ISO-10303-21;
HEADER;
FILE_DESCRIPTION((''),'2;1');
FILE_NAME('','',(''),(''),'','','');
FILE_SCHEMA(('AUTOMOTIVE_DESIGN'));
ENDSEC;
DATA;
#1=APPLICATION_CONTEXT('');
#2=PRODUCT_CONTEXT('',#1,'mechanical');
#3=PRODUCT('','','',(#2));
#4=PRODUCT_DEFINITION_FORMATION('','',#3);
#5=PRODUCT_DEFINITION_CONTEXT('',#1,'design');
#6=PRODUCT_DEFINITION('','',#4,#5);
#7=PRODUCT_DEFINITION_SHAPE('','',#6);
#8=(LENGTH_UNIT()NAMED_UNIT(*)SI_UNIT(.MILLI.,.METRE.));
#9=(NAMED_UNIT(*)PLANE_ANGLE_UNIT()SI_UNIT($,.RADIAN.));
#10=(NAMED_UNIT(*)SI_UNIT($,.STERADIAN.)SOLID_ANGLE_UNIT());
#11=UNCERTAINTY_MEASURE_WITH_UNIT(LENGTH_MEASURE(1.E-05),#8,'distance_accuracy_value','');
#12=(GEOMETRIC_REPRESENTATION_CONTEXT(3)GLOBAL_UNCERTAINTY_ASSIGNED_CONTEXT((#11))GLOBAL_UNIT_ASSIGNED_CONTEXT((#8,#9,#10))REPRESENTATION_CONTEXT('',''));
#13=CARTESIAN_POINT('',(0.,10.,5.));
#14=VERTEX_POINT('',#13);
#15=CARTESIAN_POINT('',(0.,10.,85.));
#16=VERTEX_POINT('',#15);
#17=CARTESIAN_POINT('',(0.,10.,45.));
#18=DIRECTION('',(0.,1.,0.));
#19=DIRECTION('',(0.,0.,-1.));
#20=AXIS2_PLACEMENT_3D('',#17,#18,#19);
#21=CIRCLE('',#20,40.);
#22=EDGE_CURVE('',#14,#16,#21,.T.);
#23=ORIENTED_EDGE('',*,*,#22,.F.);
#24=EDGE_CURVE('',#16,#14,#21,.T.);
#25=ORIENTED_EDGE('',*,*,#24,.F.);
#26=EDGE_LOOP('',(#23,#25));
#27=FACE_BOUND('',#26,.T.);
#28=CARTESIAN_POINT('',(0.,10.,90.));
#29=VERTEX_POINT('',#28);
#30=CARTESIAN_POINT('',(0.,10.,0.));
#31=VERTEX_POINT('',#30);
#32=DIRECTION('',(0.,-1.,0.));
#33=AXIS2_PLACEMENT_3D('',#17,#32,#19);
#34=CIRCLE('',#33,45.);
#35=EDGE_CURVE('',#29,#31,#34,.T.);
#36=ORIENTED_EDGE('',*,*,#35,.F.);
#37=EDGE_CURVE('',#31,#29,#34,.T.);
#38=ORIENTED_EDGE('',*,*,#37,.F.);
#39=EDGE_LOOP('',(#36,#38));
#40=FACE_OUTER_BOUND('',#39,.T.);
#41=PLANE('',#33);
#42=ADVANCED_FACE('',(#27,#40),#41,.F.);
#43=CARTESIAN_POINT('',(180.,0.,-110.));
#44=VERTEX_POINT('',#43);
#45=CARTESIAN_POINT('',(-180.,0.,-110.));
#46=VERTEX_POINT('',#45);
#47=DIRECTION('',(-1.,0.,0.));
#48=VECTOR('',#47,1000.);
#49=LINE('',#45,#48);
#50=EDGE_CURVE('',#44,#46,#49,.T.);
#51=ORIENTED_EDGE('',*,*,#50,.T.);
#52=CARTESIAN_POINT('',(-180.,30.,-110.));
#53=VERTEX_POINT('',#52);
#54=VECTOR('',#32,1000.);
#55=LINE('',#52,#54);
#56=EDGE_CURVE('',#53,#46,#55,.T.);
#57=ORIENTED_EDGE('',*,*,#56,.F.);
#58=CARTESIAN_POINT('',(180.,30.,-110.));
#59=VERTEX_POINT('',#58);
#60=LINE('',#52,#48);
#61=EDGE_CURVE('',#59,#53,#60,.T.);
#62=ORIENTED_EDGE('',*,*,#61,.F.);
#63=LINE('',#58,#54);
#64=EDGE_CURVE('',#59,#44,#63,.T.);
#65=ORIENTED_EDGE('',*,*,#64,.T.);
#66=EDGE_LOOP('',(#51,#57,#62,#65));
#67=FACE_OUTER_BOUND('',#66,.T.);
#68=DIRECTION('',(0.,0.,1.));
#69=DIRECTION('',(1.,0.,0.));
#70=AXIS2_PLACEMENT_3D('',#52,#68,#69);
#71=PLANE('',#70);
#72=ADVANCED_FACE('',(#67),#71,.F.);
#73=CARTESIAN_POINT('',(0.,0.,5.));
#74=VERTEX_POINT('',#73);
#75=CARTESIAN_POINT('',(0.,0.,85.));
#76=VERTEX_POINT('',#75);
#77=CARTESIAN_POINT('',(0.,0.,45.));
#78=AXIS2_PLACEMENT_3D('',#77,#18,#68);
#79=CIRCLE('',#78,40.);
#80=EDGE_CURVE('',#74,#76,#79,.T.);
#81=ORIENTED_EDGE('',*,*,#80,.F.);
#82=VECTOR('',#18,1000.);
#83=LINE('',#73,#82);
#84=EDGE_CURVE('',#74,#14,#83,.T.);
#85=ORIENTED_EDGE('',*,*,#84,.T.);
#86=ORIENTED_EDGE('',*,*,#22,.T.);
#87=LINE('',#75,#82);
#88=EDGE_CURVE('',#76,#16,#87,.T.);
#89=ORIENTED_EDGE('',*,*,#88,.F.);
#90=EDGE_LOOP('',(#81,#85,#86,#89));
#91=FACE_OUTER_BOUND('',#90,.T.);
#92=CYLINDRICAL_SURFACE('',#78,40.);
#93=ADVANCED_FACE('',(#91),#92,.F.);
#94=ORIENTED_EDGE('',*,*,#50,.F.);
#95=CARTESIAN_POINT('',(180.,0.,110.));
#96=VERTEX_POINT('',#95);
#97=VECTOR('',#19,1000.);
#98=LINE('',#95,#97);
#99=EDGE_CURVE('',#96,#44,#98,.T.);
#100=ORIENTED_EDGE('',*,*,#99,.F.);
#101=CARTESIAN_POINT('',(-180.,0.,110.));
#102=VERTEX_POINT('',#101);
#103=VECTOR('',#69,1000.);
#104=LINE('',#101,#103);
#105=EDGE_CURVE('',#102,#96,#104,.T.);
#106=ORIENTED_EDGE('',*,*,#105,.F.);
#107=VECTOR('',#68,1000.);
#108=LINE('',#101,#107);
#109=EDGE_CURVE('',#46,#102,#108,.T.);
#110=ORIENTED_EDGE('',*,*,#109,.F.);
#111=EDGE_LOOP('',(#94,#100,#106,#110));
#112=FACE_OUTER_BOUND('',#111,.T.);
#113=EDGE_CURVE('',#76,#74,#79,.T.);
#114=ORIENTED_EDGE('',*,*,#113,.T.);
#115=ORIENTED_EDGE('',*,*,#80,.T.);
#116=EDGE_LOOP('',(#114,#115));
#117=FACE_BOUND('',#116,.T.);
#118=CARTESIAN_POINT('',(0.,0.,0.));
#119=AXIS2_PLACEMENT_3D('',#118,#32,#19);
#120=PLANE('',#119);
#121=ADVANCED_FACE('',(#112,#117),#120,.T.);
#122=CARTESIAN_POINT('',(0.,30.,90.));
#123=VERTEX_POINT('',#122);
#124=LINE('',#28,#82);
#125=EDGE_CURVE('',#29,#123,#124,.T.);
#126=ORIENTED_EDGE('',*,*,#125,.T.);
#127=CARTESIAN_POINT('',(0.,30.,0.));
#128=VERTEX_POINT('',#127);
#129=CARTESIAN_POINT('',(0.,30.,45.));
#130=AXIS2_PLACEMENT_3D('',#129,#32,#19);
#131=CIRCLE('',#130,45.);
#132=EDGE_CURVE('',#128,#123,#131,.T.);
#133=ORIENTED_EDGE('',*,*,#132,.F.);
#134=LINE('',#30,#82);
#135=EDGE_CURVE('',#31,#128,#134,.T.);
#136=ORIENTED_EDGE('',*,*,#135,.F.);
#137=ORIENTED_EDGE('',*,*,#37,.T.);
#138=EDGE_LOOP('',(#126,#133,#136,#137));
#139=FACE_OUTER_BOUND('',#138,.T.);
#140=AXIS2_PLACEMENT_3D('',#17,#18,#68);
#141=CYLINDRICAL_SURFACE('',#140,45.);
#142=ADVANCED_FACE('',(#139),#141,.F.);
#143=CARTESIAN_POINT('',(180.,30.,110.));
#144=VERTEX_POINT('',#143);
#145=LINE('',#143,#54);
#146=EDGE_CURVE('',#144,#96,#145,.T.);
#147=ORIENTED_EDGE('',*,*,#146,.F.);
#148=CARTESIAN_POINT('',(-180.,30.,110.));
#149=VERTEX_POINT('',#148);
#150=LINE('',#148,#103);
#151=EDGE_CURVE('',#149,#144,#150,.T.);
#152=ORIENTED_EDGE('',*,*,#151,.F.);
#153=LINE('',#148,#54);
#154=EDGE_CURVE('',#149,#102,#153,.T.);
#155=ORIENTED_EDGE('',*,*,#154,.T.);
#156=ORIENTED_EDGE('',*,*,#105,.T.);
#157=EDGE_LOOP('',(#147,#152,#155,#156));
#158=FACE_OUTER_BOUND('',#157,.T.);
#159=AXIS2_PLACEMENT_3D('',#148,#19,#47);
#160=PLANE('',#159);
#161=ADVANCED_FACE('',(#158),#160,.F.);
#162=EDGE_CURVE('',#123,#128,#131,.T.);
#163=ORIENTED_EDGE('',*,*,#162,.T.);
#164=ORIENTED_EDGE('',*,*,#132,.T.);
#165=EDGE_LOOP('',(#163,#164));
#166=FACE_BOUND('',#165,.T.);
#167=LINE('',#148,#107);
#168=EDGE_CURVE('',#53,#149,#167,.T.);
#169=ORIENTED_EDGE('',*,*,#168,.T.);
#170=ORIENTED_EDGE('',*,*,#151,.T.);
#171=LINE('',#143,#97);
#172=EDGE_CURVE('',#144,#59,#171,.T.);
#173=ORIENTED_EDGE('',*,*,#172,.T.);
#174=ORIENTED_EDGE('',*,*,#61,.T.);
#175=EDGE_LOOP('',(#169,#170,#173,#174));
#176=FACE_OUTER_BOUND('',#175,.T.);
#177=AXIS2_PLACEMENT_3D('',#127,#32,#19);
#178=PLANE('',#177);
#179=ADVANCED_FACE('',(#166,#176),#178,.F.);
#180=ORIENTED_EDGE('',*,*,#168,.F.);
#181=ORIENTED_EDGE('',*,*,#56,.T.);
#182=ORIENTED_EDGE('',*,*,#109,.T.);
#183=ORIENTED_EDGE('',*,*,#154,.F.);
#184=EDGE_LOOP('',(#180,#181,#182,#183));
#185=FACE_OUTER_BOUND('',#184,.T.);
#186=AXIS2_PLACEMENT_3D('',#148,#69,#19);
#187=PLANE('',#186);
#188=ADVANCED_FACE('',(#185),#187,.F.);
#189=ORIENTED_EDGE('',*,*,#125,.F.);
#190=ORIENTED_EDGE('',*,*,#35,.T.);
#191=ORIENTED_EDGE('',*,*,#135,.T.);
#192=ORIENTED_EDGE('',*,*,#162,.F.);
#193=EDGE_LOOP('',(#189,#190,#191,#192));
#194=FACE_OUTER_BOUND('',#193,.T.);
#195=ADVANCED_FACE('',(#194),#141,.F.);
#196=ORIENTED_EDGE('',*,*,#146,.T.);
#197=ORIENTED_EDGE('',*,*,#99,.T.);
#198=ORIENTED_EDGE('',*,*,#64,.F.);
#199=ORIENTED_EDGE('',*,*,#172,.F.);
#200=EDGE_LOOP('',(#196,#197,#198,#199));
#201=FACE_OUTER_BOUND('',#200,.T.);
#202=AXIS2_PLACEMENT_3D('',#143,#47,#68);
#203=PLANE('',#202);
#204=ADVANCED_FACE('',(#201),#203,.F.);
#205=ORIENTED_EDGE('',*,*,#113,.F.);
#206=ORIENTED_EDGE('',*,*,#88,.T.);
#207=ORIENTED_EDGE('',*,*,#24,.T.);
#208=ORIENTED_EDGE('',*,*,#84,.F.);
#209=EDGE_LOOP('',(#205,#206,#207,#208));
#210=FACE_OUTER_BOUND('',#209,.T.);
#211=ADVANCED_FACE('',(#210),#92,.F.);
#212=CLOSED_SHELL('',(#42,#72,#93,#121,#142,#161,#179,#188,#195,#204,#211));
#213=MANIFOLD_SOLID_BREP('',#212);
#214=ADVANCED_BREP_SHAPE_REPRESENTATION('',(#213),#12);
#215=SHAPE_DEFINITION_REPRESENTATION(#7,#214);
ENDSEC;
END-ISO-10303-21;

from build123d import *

# Parameters (mm, degrees)
SKETCH_1_W          = 360
SKETCH_1_H          = 220
EXTRUDE_1_DEPTH     = 30
SKETCH_2_R          = 40
CUT_EXTRUDE_1_DEPTH = 214.072757527
SKETCH_3_R          = 45
CUT_EXTRUDE_2_DEPTH = 20


with BuildPart() as part:
    # 草图1 → 凸台-拉伸1 (new body)
    with BuildSketch(Plane(origin=(0, 0, 0), x_dir=(1, 0, 0), z_dir=(0, 1, 0))):
        Rectangle(SKETCH_1_W, SKETCH_1_H)
    extrude(amount=EXTRUDE_1_DEPTH)

    # 草图2 → 切除-拉伸1 (cut, through all)
    with BuildSketch(Plane(origin=(0, 30, 0), x_dir=(1, 0, 0), z_dir=(0, 1, 0))):
        with Locations(Location((0, -45, 0), (0, 0, 270))):
            Circle(SKETCH_2_R)
    extrude(amount=-CUT_EXTRUDE_1_DEPTH, mode=Mode.SUBTRACT)

    # 草图3 → 切除-拉伸2 (cut)
    with BuildSketch(Plane.XZ.offset(-30)):
        with Locations(Location((0, 45, 0), (0, 0, 270))):
            Circle(SKETCH_3_R)
    extrude(amount=CUT_EXTRUDE_2_DEPTH, mode=Mode.SUBTRACT)


solid = part.part
